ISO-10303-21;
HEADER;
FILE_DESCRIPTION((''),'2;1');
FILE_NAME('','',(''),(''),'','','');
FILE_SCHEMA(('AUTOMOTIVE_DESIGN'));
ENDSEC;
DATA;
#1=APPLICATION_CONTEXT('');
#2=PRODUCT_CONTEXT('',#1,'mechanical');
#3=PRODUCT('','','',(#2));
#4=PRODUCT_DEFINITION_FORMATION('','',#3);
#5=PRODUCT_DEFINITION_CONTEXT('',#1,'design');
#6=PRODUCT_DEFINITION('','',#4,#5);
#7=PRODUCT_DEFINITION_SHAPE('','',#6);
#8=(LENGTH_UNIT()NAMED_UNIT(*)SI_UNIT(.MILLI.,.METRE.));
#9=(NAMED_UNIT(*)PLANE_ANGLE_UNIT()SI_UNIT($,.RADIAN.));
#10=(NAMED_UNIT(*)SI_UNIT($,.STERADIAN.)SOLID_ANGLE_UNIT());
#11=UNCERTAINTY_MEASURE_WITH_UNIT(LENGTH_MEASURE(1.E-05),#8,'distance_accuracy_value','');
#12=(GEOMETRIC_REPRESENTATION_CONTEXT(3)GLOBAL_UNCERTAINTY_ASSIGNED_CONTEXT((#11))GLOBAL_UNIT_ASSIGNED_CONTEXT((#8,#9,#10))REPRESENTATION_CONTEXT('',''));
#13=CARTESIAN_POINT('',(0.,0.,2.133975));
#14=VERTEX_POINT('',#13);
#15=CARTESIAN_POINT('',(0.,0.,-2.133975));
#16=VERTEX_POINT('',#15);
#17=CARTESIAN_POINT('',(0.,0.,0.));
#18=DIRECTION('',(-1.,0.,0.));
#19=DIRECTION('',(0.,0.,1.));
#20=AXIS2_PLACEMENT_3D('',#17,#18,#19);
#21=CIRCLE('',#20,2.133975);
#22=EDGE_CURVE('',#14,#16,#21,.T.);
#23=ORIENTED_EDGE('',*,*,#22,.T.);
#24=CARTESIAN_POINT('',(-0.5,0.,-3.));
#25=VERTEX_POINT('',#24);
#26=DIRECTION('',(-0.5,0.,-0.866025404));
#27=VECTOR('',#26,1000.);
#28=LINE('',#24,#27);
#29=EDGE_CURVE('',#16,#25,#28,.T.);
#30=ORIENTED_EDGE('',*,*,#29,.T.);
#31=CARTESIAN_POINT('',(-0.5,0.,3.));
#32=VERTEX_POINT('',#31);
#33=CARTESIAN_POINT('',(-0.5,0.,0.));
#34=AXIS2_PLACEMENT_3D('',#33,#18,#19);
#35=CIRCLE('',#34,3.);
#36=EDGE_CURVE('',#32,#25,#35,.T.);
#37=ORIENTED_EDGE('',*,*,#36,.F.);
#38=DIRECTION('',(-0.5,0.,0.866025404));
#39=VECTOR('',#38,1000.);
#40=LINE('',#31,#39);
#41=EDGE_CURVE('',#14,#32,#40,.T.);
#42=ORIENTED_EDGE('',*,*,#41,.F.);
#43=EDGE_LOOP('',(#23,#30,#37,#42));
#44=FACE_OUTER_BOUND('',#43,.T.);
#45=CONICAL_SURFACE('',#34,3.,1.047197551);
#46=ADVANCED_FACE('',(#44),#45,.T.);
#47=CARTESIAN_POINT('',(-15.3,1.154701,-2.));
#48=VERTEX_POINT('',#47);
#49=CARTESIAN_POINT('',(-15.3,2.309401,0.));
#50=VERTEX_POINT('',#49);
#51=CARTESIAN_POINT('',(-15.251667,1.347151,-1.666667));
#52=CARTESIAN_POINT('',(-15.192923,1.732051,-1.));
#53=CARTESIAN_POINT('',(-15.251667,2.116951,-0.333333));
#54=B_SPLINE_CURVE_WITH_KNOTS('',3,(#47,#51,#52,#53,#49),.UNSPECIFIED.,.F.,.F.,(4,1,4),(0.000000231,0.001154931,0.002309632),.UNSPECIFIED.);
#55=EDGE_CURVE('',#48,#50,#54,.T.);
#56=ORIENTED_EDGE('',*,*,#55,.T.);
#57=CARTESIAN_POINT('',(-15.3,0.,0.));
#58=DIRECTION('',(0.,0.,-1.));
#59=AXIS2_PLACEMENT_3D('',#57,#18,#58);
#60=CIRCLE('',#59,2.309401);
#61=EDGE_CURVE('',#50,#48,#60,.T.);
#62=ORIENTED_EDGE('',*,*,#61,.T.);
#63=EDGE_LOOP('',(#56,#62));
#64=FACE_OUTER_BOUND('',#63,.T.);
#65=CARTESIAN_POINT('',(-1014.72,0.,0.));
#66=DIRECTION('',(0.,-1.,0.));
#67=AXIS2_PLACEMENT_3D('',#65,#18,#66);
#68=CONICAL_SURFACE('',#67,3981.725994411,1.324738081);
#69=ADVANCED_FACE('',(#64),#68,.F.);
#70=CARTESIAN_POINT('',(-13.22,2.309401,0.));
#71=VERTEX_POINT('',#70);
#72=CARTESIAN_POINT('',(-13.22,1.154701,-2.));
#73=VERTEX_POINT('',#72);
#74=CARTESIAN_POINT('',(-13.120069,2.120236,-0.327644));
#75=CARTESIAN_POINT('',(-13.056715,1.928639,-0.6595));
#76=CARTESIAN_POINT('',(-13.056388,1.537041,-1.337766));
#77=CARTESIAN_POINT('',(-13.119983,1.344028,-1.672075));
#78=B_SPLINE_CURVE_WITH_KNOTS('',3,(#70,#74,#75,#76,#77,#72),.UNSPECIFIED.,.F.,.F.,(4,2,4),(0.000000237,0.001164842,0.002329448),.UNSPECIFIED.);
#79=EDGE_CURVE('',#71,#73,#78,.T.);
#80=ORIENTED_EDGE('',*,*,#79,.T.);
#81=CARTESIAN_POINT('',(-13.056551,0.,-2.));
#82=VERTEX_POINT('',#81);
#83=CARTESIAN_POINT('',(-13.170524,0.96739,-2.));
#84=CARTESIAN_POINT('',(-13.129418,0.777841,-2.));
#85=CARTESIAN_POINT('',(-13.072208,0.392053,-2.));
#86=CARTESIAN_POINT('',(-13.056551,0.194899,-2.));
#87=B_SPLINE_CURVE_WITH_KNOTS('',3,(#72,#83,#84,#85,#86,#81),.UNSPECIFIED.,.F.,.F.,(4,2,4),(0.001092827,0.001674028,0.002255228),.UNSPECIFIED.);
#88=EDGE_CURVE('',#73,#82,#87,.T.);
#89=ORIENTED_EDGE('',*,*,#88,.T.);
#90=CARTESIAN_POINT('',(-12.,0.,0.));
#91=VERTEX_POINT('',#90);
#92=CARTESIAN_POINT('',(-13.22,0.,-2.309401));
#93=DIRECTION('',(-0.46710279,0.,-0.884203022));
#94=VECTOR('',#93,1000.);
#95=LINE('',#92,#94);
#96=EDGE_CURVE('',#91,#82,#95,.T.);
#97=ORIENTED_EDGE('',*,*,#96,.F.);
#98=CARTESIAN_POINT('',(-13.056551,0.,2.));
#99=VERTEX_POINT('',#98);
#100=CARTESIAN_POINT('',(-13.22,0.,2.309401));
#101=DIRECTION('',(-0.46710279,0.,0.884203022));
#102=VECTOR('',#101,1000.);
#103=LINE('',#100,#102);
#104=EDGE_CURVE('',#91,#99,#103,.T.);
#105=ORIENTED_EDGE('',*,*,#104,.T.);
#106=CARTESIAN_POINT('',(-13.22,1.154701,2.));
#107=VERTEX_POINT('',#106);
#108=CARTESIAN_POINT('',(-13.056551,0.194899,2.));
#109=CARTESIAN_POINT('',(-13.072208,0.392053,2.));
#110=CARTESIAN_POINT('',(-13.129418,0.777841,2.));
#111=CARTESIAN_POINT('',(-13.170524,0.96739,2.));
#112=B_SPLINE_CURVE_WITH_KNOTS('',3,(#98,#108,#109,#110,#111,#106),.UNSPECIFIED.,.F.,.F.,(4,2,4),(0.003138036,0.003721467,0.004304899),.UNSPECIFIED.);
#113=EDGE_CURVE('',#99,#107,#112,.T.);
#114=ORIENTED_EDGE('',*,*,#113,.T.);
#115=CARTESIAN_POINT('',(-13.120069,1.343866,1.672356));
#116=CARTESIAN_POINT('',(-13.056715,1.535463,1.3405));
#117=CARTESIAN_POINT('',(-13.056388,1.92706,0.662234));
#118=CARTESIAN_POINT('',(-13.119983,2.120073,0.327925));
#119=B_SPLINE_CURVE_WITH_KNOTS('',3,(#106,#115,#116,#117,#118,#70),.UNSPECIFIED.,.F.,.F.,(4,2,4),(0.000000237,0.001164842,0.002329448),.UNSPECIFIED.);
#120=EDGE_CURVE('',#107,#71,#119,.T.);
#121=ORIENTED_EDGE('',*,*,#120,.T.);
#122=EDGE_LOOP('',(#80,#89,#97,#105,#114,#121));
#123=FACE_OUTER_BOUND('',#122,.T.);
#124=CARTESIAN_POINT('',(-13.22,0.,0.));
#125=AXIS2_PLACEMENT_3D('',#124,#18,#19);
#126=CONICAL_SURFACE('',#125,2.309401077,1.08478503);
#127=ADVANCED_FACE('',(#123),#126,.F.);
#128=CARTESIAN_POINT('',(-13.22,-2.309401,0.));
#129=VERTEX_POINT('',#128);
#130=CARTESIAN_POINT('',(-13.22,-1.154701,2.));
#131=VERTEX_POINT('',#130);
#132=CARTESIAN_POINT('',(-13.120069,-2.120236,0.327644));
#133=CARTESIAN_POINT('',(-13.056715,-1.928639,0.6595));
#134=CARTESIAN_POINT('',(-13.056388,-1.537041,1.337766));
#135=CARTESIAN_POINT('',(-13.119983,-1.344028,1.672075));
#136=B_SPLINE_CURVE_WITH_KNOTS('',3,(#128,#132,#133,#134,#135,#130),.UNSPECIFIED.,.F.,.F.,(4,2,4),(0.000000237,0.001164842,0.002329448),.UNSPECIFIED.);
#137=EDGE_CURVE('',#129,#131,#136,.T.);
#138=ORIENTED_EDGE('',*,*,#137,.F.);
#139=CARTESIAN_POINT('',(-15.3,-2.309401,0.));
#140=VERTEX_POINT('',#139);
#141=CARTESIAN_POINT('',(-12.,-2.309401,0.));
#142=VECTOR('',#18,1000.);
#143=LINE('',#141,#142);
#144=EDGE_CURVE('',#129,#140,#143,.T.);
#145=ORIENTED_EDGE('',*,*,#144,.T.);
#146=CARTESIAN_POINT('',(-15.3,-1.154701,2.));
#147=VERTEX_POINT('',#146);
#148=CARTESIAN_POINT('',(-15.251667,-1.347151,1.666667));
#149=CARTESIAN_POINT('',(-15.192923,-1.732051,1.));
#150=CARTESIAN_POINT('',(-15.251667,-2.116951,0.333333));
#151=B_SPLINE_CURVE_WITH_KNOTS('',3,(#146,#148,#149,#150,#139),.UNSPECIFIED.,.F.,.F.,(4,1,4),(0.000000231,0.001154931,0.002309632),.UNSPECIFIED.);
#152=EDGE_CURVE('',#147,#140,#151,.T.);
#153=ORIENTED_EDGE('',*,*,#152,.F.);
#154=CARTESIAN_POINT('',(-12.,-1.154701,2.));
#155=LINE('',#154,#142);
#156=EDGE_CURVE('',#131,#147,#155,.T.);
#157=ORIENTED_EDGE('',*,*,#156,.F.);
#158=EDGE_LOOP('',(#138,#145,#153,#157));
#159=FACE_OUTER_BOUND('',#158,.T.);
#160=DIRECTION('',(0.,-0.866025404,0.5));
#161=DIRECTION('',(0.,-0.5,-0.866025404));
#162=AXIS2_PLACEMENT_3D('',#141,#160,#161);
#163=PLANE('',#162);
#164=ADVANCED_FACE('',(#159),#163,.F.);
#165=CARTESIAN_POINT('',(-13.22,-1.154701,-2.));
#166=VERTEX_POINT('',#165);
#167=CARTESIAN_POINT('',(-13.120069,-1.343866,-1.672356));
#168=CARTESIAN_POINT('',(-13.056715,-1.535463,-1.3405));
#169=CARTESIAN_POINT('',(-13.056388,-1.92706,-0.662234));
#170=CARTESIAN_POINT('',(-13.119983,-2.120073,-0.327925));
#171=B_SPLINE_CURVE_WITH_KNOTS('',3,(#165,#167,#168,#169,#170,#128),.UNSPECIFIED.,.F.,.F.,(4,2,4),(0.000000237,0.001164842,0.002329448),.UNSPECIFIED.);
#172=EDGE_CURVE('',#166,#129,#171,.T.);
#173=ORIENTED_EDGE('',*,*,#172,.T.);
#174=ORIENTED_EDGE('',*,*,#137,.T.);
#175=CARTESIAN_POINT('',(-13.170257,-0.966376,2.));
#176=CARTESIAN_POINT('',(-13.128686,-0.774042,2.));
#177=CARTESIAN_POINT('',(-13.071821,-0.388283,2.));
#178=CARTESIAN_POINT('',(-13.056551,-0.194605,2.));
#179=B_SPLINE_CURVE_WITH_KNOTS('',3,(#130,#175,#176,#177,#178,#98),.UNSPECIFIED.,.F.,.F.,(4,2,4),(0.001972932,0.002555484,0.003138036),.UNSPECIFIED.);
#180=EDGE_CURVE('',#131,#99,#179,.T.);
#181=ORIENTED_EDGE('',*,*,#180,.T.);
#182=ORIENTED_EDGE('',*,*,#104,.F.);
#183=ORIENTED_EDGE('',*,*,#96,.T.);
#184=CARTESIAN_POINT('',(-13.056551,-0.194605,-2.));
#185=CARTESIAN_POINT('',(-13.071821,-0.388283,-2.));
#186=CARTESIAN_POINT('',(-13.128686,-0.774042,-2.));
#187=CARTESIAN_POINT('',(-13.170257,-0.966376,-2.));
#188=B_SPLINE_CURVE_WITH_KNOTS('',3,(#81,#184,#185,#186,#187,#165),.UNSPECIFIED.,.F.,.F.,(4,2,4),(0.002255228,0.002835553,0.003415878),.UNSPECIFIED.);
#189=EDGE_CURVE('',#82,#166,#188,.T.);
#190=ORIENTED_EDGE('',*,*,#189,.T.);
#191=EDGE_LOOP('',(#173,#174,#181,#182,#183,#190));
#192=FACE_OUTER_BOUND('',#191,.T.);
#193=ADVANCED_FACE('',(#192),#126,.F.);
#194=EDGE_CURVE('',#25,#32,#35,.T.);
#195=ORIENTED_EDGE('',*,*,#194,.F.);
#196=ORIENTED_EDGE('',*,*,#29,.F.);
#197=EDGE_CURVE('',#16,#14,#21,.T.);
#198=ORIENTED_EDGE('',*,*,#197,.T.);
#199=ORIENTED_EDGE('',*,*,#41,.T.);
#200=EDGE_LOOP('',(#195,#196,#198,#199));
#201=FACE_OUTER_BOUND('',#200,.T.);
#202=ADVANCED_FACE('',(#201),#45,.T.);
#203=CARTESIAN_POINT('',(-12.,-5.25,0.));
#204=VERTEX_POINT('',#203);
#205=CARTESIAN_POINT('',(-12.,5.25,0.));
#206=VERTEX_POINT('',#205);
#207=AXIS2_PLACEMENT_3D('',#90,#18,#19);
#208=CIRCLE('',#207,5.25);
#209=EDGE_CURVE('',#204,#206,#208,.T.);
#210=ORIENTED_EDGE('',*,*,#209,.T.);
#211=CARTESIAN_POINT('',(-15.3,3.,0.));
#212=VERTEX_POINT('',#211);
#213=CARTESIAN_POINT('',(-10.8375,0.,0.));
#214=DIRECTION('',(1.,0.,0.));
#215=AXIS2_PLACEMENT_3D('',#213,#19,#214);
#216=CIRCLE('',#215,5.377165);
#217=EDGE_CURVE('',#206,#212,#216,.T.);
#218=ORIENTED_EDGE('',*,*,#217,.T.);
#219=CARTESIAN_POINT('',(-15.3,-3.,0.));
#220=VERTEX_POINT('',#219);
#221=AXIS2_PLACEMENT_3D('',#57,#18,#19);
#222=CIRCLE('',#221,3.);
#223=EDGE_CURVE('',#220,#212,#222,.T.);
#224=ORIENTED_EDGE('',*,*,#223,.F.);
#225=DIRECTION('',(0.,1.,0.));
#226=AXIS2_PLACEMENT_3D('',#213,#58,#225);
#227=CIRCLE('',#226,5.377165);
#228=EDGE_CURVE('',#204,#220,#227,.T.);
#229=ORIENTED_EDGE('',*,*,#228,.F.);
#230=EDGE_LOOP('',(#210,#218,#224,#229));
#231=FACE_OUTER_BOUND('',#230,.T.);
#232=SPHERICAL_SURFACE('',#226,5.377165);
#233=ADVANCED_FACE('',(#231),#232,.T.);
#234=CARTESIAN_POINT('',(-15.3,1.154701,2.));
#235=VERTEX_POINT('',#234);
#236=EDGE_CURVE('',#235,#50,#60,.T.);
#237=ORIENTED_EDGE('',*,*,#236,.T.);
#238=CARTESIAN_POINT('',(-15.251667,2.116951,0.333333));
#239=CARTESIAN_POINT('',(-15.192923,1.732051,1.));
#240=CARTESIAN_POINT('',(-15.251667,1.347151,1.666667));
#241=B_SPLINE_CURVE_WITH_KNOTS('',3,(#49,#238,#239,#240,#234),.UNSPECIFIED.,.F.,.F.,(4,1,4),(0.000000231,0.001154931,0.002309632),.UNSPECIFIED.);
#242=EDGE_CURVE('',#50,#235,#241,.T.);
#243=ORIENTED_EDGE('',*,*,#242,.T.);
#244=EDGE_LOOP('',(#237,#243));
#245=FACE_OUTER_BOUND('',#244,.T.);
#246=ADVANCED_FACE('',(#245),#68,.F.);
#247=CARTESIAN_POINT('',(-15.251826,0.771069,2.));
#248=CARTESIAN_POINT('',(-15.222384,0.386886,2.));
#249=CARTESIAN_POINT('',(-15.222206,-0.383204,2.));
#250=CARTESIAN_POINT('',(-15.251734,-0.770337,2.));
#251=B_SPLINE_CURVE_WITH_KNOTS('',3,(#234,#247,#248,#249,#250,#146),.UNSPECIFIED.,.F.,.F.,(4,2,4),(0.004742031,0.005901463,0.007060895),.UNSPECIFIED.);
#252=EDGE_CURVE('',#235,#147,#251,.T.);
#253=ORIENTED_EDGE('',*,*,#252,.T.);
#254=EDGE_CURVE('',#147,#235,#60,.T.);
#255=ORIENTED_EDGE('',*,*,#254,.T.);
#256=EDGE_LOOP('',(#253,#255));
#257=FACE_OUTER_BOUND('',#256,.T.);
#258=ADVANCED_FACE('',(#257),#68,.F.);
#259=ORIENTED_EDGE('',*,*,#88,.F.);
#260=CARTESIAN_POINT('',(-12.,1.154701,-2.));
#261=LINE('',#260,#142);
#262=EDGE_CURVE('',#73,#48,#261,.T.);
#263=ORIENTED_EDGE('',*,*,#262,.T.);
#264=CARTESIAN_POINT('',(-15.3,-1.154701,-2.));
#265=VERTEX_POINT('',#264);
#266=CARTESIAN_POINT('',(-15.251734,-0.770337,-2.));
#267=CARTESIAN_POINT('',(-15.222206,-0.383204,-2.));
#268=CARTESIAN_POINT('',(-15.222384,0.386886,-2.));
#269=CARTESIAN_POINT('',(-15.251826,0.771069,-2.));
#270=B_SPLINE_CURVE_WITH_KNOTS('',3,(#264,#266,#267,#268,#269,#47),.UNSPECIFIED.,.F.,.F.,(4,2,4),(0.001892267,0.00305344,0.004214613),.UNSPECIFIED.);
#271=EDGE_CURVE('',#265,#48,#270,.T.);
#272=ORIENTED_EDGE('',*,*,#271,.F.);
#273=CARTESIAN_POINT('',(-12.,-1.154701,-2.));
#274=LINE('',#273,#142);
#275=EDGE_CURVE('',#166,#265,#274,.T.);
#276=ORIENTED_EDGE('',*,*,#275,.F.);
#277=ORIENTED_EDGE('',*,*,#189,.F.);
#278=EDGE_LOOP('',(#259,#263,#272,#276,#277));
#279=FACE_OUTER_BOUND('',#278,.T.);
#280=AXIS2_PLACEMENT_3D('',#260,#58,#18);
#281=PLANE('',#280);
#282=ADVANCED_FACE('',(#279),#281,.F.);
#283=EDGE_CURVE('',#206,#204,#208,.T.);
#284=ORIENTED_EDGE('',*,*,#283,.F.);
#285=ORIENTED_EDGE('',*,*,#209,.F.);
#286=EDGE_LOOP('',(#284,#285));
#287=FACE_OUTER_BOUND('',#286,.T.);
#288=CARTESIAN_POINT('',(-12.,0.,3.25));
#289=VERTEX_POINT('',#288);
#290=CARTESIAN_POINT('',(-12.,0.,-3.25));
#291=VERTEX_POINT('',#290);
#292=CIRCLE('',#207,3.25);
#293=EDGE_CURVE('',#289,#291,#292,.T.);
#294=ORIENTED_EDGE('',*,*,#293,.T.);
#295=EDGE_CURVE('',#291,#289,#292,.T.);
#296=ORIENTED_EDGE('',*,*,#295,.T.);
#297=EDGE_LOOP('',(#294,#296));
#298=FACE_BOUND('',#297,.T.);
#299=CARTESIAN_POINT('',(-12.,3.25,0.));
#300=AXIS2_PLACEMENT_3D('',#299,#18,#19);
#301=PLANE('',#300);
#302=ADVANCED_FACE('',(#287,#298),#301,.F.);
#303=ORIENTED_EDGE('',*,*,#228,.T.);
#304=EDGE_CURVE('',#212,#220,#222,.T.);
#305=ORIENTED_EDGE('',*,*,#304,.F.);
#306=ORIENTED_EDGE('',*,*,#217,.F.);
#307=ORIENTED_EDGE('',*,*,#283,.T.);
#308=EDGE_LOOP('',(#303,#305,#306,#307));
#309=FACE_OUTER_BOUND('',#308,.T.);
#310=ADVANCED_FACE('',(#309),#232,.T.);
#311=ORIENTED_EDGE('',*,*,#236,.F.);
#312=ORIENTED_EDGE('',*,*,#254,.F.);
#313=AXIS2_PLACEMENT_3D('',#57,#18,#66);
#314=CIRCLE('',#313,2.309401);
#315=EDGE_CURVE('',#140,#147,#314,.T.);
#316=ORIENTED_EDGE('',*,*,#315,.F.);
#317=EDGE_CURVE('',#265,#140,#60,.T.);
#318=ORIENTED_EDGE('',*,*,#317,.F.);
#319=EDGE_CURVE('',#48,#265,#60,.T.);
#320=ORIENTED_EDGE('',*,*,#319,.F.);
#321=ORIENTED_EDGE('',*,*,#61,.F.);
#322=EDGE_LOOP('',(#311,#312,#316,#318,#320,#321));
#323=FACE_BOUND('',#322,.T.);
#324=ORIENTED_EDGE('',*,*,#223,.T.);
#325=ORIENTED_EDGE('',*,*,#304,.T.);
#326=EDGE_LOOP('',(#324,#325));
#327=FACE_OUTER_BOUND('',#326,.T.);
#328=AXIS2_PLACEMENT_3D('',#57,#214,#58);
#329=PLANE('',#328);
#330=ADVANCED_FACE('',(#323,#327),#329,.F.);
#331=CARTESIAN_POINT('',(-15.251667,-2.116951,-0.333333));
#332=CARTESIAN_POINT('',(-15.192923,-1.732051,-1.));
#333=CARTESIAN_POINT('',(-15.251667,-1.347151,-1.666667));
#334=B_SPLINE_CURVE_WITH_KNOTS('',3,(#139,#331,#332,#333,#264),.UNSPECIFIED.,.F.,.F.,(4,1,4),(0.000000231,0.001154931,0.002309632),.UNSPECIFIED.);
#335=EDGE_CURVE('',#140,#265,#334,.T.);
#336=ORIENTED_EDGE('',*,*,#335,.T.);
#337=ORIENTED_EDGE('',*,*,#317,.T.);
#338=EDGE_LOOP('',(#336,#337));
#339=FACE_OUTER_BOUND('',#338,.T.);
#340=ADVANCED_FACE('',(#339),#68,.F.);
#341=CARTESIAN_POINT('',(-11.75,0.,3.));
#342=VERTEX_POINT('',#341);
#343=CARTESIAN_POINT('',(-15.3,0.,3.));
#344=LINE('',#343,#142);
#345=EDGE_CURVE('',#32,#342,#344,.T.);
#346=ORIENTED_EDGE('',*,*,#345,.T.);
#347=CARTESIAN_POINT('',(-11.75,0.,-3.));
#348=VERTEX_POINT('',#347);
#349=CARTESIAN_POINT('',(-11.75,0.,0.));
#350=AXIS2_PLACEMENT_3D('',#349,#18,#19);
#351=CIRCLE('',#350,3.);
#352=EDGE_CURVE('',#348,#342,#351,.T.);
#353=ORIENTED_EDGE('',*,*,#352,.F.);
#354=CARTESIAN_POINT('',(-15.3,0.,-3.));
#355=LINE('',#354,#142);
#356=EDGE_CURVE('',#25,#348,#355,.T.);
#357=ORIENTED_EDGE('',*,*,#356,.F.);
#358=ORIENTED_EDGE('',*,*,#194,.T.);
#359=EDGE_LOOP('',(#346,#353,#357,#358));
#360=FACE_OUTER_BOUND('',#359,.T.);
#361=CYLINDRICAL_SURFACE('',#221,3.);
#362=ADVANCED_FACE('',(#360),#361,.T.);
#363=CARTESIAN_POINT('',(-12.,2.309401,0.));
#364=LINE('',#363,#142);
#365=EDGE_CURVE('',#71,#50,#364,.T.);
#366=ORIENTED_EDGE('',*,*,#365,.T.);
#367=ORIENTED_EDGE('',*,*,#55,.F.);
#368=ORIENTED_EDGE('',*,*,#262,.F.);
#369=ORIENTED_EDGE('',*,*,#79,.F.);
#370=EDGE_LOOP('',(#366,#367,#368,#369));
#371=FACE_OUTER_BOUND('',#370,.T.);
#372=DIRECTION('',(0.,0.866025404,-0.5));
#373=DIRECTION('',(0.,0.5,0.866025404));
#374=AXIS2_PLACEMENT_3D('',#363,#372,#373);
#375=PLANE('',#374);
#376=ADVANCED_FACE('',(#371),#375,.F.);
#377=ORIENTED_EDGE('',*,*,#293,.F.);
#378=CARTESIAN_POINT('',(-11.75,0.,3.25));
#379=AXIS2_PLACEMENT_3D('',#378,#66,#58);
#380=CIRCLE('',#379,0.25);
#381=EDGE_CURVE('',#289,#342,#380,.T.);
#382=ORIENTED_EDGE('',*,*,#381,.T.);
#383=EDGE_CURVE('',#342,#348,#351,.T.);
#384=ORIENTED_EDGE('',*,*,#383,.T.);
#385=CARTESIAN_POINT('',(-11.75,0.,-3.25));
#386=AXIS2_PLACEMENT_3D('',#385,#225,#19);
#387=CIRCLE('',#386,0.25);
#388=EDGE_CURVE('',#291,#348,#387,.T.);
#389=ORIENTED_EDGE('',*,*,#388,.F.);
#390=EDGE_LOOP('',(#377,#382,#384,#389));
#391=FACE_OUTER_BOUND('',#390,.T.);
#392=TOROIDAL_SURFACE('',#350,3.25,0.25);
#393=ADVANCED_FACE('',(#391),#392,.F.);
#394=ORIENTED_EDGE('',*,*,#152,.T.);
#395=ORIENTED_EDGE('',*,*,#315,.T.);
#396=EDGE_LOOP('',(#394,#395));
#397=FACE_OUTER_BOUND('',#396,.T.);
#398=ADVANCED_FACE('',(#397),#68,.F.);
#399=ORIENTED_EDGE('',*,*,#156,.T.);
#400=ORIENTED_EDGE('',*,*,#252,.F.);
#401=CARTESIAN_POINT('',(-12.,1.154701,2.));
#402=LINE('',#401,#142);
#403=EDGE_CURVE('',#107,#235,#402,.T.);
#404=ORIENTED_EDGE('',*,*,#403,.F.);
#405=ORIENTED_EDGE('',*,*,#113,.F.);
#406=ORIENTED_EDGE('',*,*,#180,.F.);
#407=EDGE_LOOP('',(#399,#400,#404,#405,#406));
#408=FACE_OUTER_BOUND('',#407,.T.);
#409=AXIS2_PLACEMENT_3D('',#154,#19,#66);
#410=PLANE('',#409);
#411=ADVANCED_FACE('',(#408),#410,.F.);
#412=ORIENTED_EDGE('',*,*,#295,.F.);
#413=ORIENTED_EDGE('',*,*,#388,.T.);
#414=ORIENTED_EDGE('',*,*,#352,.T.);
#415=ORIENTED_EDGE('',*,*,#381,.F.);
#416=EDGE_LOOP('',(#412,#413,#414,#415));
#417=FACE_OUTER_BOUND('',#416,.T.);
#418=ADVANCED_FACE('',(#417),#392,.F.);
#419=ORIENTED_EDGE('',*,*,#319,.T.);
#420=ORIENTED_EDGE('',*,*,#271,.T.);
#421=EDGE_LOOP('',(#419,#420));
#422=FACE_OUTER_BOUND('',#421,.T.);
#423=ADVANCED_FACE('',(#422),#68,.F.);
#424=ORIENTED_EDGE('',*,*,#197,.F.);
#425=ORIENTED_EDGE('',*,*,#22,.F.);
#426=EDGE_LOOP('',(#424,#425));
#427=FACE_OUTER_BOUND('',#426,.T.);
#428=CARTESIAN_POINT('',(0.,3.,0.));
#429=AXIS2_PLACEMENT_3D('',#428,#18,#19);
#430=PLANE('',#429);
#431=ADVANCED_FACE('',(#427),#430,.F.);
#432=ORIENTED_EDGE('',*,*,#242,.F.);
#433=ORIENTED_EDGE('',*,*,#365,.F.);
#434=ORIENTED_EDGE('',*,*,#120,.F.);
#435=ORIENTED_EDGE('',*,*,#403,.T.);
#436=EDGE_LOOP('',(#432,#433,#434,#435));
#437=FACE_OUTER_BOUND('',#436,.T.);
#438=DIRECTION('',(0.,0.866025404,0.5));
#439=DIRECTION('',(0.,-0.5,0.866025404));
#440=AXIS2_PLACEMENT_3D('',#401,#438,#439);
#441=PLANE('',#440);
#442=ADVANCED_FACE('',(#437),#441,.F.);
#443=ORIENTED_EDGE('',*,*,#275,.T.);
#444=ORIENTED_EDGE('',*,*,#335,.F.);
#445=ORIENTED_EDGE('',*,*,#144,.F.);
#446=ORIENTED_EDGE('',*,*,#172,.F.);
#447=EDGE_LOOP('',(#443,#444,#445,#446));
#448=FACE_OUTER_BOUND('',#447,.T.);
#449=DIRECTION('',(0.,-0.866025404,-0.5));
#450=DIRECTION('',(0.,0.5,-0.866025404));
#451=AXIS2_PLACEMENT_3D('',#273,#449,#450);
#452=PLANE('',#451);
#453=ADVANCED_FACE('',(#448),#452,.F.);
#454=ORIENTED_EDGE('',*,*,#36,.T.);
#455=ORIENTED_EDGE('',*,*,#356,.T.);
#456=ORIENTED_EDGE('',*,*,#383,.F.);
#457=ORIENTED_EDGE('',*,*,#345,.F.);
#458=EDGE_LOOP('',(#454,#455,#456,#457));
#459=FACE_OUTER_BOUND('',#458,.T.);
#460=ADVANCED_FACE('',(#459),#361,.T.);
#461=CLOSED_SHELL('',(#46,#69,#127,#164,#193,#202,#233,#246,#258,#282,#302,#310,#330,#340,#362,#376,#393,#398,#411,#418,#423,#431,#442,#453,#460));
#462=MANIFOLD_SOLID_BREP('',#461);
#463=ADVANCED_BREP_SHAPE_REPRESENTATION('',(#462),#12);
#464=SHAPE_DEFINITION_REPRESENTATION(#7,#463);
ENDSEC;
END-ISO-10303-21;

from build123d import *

# Parameters (mm, degrees)
CUT_EXTRUDE1_DEPTH = 3.3


with BuildPart() as part:
    # Sketch1 → Revolve1 (revolve)
    with BuildSketch(Plane.XY, mode=Mode.PRIVATE) as revolve1_sk:
        with BuildLine():
            Line((0, 3), (-11.75, 3))
            ThreePointArc((-11.75, 3), (-11.926776695, 3.073223305), (-12, 3.25))
            Line((-12, 3.25), (-12, 5.25))
            ThreePointArc((-12, 5.25), (-13.866655204, 4.442760966), (-15.3, 3))
            Line((-15.3, 3), (-15.3, 0))
            Line((-15.3, 0), (0, 0))
            Line((0, 0), (0, 3))
        make_face()
    revolve(revolve1_sk.sketch.rotate(Axis((-15.3, 0, 0), (1, 0, 0)), 90), axis=Axis((-15.3, 0, 0), (1, 0, 0)))

    # Sketch2 → Cut-Extrude1 (cut)
    with BuildSketch(Plane.ZY.offset(15.3)):
        Polygon((0, 2.309401077), (-2, 1.154700538), (-2, -1.154700538), (0, -2.309401077), (2, -1.154700538), (2, 1.154700538), align=None)
    extrude(amount=-CUT_EXTRUDE1_DEPTH, mode=Mode.SUBTRACT)

    # Sketch6 → Revolve2 (revolve)
    with BuildSketch(Plane.XY):
        Polygon((-13.22, 2.309401077), (-12, 0), (-11.42, 0), (-11.42, 2.309401077), align=None)
    revolve(axis=Axis((-15.3, 0, 0), (1, 0, 0)))

    # Sketch7 → Cut-Revolve5 (revolve, cut)
    with BuildSketch(Plane.XY):
        Polygon((-15.3, 2.309401077), (-14.72, 0), (-15.3, 0), align=None)
    revolve(axis=Axis((-15.3, 0, 0), (1, 0, 0)), mode=Mode.SUBTRACT)

    # Sketch4 → Cut-Revolve1 (revolve, cut)
    with BuildSketch(Plane.XY, mode=Mode.PRIVATE) as cut_revolve1_sk:
        Polygon((-0.5, 3), (0, 2.133974596), (0.5, 3), align=None)
    revolve(cut_revolve1_sk.sketch.rotate(Axis((-0.5, 0, 0), (1, 0, 0)), 90), axis=Axis((-0.5, 0, 0), (1, 0, 0)), mode=Mode.SUBTRACT)


solid = part.part
